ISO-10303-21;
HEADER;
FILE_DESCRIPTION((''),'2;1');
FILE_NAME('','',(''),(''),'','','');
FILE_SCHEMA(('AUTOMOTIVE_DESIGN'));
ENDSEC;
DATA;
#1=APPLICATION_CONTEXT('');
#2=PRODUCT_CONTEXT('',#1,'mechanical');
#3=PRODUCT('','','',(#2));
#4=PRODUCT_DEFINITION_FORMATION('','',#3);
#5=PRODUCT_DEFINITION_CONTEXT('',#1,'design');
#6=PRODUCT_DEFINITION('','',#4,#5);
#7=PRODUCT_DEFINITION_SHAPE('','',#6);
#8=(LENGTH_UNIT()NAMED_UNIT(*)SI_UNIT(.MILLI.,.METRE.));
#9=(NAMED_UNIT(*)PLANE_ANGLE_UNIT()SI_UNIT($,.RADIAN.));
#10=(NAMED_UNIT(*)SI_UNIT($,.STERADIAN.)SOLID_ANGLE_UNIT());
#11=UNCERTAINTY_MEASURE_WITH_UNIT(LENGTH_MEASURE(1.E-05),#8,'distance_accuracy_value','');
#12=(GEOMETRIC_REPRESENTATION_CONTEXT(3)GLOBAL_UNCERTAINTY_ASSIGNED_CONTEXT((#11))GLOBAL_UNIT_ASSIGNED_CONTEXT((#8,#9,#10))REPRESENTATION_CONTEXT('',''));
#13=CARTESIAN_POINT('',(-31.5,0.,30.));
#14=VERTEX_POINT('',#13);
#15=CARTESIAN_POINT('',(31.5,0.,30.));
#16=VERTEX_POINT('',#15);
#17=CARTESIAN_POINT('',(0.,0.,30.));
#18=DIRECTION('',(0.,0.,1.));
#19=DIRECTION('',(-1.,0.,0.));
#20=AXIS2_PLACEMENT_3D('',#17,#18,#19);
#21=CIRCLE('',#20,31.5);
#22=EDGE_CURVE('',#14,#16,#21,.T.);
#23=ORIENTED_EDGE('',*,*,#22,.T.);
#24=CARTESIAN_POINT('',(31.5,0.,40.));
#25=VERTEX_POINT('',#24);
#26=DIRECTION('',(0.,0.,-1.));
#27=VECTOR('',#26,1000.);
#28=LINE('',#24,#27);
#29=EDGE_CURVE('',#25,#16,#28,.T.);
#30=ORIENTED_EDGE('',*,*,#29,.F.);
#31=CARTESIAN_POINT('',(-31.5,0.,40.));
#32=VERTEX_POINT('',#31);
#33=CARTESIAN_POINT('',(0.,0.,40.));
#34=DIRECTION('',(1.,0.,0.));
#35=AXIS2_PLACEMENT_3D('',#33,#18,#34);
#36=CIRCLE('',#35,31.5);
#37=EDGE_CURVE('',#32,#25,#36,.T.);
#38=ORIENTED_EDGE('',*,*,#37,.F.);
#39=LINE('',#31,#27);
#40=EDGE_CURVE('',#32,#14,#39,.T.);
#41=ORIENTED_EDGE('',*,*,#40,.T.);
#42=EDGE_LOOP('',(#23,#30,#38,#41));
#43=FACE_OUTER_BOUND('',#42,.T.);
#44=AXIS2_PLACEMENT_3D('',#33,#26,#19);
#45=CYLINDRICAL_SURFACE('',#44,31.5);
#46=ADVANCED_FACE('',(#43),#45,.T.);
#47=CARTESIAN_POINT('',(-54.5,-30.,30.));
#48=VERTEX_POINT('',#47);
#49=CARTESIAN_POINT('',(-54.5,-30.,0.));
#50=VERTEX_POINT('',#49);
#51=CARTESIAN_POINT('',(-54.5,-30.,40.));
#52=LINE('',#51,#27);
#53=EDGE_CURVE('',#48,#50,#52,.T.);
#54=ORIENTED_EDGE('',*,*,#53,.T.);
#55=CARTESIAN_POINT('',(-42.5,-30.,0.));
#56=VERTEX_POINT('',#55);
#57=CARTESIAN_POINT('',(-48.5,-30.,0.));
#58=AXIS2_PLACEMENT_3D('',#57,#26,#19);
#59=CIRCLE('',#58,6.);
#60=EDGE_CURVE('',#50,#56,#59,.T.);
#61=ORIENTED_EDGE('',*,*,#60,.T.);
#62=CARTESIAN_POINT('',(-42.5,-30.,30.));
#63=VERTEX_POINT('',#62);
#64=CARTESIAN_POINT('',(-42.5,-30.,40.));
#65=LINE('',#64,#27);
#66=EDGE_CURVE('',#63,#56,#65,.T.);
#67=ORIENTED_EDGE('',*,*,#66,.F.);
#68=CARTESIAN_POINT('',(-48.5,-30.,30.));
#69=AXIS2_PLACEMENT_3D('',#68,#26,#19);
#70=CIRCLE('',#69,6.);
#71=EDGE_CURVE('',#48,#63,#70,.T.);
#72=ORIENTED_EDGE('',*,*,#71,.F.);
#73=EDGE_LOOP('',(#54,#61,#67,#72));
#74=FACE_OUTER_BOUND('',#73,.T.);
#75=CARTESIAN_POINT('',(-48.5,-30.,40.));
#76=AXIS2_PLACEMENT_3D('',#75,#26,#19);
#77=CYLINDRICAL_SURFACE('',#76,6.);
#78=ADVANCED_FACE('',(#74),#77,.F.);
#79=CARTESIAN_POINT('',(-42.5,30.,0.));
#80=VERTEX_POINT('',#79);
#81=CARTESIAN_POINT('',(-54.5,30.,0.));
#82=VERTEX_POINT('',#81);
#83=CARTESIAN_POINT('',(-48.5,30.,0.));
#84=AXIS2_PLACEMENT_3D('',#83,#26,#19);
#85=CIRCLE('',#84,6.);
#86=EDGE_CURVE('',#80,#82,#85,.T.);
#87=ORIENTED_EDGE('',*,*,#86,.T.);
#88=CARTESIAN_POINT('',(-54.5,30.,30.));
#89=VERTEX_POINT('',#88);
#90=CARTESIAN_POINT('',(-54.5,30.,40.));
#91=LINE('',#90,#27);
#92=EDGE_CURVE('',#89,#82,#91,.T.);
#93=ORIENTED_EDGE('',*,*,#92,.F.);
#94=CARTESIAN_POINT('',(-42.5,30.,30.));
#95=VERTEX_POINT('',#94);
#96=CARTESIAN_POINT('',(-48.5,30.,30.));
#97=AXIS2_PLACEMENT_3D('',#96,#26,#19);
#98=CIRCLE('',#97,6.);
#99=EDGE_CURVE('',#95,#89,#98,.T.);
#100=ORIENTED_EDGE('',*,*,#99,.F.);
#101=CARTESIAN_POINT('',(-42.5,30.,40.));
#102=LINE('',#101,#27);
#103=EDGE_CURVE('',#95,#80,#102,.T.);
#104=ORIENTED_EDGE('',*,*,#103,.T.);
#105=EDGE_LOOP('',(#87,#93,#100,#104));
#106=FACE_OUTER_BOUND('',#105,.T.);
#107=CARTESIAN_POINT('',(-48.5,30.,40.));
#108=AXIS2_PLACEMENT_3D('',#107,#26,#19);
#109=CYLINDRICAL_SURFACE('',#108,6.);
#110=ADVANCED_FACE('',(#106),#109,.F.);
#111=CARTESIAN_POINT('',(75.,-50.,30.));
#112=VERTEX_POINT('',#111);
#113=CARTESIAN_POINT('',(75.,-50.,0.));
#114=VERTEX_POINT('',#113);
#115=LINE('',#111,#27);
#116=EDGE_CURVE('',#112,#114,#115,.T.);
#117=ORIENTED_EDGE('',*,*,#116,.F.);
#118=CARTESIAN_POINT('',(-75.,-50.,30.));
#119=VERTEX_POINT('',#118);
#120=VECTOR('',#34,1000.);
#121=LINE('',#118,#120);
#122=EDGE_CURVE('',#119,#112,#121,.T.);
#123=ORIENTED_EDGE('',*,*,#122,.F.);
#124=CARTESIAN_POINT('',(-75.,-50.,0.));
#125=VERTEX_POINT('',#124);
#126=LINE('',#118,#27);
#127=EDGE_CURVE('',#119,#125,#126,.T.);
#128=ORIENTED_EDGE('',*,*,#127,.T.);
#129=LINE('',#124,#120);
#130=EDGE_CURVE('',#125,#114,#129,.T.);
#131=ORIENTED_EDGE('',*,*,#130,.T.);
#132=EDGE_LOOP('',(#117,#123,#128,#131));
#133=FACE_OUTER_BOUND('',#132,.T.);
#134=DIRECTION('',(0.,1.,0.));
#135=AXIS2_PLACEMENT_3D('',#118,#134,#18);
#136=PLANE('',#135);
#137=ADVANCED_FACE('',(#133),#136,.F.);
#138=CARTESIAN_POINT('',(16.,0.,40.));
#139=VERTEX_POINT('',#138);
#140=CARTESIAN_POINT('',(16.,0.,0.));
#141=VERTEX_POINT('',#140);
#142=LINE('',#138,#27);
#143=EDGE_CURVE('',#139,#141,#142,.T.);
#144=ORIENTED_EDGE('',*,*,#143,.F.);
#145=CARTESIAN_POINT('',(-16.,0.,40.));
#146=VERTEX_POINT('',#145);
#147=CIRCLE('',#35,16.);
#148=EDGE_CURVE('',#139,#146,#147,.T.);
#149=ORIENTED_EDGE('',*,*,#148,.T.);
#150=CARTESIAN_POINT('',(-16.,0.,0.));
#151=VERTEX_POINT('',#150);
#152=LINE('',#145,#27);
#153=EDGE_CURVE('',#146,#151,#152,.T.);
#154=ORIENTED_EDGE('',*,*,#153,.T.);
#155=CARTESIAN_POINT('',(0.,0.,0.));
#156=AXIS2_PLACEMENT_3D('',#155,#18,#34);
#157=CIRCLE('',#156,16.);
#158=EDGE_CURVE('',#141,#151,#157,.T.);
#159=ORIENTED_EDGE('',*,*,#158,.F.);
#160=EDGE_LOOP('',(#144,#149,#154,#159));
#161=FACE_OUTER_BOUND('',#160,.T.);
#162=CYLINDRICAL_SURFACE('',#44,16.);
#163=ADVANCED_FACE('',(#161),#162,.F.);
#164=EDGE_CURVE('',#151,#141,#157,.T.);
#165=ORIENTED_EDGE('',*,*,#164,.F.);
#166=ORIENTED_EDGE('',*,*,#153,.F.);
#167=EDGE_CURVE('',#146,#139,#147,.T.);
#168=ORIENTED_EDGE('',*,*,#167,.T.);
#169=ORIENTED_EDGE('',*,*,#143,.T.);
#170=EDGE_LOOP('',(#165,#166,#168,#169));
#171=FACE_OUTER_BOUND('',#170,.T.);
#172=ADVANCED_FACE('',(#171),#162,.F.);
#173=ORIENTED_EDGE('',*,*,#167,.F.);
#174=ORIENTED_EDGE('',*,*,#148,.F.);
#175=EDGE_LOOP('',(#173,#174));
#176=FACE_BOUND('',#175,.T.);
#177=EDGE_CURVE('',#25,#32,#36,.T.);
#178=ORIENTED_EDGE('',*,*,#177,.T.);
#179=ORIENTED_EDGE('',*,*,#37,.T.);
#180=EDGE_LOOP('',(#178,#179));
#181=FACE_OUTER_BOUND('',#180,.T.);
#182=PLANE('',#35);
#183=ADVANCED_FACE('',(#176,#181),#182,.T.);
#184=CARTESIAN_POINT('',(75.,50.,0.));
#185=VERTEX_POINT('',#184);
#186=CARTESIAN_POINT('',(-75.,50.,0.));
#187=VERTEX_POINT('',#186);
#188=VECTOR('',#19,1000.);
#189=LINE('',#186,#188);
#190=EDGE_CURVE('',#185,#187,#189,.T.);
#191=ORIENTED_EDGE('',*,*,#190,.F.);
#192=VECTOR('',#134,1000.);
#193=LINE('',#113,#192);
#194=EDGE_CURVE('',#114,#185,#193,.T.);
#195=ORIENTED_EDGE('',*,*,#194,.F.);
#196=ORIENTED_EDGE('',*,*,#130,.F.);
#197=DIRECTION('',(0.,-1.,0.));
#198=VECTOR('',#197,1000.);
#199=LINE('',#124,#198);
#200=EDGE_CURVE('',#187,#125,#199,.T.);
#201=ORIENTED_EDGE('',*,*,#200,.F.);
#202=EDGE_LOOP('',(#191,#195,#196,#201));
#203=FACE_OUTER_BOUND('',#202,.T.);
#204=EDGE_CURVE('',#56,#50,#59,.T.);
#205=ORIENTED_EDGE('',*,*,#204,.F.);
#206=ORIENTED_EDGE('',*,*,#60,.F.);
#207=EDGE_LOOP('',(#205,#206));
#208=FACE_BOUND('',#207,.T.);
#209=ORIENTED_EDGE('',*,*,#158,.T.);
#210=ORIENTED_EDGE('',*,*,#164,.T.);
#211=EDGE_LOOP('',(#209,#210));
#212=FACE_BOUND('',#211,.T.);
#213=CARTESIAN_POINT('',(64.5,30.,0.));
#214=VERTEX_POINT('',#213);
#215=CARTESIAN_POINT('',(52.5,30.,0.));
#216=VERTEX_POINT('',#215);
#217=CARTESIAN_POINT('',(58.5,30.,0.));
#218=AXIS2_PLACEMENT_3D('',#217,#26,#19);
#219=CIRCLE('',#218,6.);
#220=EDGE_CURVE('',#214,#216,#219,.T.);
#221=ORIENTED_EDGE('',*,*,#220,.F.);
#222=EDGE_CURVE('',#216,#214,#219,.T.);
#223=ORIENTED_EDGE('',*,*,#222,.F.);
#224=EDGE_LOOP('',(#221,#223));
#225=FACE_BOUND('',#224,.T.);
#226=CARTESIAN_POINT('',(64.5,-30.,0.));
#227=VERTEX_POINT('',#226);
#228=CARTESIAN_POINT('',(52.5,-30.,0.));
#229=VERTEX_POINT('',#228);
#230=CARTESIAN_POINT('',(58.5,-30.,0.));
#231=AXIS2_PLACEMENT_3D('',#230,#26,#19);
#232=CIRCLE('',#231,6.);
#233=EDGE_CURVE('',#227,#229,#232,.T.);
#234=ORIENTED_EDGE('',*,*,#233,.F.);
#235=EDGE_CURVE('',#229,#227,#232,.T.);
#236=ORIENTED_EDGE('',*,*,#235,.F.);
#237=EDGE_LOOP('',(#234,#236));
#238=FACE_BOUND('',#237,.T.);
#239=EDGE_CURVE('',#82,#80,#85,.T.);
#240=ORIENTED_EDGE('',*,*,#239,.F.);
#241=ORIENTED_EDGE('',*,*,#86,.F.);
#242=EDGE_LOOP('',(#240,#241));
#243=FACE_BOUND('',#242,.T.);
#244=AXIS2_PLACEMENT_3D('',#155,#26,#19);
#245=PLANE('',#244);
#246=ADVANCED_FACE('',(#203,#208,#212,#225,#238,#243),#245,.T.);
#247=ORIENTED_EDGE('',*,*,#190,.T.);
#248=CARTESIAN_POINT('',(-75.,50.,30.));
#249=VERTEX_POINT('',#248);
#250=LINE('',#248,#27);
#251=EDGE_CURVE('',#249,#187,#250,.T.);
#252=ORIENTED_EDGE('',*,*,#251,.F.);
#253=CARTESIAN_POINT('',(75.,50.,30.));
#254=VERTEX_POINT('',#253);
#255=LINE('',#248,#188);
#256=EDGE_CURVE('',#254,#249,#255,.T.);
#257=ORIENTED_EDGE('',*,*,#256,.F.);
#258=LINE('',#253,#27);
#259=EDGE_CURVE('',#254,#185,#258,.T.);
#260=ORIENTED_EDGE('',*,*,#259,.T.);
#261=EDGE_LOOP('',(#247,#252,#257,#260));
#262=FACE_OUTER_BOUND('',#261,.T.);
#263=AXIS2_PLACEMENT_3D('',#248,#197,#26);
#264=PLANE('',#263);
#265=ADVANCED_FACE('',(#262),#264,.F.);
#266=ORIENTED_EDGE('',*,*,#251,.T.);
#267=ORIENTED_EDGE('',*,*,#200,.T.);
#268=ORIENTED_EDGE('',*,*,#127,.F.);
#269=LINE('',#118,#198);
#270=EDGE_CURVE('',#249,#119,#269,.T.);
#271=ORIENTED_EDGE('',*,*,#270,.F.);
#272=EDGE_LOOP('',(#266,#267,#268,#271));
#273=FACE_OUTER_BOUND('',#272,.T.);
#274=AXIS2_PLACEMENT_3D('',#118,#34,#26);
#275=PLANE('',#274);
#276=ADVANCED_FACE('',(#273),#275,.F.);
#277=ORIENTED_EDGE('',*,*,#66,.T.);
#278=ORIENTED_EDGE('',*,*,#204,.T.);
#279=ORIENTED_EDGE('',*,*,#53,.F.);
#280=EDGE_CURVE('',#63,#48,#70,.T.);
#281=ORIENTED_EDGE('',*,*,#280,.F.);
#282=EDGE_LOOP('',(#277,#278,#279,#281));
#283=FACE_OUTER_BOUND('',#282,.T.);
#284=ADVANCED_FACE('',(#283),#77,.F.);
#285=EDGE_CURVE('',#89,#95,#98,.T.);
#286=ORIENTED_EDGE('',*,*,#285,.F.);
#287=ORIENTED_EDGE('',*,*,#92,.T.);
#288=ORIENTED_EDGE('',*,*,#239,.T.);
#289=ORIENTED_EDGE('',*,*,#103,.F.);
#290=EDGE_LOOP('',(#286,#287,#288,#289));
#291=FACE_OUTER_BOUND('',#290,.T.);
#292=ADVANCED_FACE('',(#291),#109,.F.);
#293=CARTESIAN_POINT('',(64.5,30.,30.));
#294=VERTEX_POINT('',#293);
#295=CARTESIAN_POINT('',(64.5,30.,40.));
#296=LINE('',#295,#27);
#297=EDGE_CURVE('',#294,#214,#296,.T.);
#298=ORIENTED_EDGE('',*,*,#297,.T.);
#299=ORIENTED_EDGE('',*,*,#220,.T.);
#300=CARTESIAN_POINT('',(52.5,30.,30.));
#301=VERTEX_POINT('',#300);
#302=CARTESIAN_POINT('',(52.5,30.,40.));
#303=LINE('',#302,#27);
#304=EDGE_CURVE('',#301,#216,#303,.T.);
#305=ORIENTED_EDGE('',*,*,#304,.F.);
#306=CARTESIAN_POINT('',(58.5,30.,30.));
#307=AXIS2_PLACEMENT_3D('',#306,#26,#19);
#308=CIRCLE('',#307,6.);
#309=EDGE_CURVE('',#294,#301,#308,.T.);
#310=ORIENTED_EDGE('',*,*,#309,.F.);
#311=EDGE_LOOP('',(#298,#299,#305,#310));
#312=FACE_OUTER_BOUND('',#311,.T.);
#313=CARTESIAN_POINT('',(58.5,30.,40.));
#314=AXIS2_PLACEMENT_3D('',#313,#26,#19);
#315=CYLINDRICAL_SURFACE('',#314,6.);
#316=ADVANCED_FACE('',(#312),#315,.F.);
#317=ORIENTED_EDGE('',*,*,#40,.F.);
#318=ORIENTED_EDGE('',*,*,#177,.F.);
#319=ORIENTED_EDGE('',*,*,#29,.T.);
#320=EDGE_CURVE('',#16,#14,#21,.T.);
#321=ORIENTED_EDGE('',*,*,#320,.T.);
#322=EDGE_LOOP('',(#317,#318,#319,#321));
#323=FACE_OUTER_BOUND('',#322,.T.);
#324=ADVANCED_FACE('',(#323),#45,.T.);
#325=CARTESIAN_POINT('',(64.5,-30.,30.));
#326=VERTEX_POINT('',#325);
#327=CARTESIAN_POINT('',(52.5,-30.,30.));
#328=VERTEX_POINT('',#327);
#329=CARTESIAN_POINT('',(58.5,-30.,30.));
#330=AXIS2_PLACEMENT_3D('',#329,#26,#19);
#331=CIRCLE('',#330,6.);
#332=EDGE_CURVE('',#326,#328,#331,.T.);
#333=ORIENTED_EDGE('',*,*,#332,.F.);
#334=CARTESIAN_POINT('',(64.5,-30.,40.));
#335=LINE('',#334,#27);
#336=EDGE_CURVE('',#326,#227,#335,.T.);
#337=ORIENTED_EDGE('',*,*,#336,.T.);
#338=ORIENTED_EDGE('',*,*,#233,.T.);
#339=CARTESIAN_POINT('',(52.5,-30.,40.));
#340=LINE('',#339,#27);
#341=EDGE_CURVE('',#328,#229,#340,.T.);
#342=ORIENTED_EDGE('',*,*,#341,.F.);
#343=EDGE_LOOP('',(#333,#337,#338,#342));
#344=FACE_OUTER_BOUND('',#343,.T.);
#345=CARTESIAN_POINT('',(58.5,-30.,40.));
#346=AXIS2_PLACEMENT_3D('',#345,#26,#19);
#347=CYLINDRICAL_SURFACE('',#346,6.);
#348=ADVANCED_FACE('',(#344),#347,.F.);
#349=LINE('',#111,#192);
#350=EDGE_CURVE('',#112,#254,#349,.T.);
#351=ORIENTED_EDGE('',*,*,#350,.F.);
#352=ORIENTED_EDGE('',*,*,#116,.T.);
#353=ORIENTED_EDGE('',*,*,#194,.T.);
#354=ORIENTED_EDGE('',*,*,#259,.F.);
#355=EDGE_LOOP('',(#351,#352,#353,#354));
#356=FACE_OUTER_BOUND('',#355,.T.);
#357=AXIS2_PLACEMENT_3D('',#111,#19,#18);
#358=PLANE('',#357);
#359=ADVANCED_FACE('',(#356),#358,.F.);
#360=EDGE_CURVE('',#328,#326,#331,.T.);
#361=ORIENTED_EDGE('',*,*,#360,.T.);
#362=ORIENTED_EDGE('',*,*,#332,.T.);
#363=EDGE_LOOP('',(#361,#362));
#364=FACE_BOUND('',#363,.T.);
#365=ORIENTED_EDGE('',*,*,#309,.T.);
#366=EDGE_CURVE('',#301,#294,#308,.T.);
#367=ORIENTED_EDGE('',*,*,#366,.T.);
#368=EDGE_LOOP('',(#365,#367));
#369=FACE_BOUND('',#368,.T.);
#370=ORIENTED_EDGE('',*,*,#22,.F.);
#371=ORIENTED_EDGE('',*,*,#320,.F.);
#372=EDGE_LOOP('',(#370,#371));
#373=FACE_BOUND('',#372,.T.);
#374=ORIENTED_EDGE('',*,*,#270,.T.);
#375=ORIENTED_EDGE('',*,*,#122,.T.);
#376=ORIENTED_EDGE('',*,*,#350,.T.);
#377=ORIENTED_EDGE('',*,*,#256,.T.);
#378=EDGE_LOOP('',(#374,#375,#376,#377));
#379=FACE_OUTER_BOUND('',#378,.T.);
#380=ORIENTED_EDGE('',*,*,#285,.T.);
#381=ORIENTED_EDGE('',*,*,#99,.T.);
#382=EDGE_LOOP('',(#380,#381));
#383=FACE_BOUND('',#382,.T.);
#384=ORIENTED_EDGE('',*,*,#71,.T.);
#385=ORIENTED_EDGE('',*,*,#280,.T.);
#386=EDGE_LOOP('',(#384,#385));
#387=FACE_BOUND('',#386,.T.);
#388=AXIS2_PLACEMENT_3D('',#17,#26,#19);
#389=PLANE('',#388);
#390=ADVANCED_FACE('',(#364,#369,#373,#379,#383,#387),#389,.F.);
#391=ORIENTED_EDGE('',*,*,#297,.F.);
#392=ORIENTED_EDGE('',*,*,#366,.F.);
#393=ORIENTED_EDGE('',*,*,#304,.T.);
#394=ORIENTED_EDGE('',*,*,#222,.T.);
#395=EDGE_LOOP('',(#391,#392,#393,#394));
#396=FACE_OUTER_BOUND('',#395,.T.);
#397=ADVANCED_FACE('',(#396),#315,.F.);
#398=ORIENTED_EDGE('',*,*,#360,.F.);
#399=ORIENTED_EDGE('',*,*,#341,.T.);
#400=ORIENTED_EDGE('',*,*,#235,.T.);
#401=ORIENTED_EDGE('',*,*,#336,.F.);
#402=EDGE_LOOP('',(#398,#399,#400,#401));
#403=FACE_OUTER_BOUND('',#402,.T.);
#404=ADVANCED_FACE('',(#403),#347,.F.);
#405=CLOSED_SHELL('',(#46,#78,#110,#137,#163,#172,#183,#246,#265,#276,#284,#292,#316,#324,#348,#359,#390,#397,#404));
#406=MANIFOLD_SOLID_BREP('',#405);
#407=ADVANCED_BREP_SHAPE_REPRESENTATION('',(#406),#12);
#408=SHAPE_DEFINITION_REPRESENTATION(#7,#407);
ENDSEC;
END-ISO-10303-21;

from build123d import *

# Parameters (mm, degrees)
SKETCH_1_W          = 150
SKETCH_1_H          = 100
EXTRUDE_1_DEPTH     = 30
SKETCH_2_R          = 31.5
SKETCH_2_R_2        = 16
EXTRUDE_2_DEPTH     = 10
SKETCH_3_R          = 16
CUT_EXTRUDE_1_DEPTH = 96
SKETCH_4_R          = 6
CUT_EXTRUDE_2_DEPTH = 99.615414617


with BuildPart() as part:
    # 草图1 → 凸台-拉伸1 (new body)
    with BuildSketch(Plane.XY):
        Rectangle(SKETCH_1_W, SKETCH_1_H)
    extrude(amount=EXTRUDE_1_DEPTH)

    # 草图2 → 凸台-拉伸2 (add)
    with BuildSketch(Plane.XY.offset(30)):
        with Locations(Location((0, 0, 0), (0, 0, 180))):
            Circle(SKETCH_2_R)
        Circle(SKETCH_2_R_2, mode=Mode.SUBTRACT)
    extrude(amount=EXTRUDE_2_DEPTH)

    # 草图3 → 切除-拉伸1 (cut, through all)
    with BuildSketch(Plane.XY.offset(30)):
        Circle(SKETCH_3_R)
    extrude(amount=-CUT_EXTRUDE_1_DEPTH, mode=Mode.SUBTRACT)

    # 草图4 → 切除-拉伸2 (cut, through all)
    with BuildSketch(Plane(origin=(0, 0, 0), x_dir=(-1, 0, 0), z_dir=(0, 0, -1))):
        with Locations((-58.5, 30)):
            Circle(SKETCH_4_R)
        with Locations((48.5, 30)):
            Circle(SKETCH_4_R)
        with Locations((48.5, -30)):
            Circle(SKETCH_4_R)
        with Locations((-58.5, -30)):
            Circle(SKETCH_4_R)
    extrude(amount=-CUT_EXTRUDE_2_DEPTH, mode=Mode.SUBTRACT)


solid = part.part
